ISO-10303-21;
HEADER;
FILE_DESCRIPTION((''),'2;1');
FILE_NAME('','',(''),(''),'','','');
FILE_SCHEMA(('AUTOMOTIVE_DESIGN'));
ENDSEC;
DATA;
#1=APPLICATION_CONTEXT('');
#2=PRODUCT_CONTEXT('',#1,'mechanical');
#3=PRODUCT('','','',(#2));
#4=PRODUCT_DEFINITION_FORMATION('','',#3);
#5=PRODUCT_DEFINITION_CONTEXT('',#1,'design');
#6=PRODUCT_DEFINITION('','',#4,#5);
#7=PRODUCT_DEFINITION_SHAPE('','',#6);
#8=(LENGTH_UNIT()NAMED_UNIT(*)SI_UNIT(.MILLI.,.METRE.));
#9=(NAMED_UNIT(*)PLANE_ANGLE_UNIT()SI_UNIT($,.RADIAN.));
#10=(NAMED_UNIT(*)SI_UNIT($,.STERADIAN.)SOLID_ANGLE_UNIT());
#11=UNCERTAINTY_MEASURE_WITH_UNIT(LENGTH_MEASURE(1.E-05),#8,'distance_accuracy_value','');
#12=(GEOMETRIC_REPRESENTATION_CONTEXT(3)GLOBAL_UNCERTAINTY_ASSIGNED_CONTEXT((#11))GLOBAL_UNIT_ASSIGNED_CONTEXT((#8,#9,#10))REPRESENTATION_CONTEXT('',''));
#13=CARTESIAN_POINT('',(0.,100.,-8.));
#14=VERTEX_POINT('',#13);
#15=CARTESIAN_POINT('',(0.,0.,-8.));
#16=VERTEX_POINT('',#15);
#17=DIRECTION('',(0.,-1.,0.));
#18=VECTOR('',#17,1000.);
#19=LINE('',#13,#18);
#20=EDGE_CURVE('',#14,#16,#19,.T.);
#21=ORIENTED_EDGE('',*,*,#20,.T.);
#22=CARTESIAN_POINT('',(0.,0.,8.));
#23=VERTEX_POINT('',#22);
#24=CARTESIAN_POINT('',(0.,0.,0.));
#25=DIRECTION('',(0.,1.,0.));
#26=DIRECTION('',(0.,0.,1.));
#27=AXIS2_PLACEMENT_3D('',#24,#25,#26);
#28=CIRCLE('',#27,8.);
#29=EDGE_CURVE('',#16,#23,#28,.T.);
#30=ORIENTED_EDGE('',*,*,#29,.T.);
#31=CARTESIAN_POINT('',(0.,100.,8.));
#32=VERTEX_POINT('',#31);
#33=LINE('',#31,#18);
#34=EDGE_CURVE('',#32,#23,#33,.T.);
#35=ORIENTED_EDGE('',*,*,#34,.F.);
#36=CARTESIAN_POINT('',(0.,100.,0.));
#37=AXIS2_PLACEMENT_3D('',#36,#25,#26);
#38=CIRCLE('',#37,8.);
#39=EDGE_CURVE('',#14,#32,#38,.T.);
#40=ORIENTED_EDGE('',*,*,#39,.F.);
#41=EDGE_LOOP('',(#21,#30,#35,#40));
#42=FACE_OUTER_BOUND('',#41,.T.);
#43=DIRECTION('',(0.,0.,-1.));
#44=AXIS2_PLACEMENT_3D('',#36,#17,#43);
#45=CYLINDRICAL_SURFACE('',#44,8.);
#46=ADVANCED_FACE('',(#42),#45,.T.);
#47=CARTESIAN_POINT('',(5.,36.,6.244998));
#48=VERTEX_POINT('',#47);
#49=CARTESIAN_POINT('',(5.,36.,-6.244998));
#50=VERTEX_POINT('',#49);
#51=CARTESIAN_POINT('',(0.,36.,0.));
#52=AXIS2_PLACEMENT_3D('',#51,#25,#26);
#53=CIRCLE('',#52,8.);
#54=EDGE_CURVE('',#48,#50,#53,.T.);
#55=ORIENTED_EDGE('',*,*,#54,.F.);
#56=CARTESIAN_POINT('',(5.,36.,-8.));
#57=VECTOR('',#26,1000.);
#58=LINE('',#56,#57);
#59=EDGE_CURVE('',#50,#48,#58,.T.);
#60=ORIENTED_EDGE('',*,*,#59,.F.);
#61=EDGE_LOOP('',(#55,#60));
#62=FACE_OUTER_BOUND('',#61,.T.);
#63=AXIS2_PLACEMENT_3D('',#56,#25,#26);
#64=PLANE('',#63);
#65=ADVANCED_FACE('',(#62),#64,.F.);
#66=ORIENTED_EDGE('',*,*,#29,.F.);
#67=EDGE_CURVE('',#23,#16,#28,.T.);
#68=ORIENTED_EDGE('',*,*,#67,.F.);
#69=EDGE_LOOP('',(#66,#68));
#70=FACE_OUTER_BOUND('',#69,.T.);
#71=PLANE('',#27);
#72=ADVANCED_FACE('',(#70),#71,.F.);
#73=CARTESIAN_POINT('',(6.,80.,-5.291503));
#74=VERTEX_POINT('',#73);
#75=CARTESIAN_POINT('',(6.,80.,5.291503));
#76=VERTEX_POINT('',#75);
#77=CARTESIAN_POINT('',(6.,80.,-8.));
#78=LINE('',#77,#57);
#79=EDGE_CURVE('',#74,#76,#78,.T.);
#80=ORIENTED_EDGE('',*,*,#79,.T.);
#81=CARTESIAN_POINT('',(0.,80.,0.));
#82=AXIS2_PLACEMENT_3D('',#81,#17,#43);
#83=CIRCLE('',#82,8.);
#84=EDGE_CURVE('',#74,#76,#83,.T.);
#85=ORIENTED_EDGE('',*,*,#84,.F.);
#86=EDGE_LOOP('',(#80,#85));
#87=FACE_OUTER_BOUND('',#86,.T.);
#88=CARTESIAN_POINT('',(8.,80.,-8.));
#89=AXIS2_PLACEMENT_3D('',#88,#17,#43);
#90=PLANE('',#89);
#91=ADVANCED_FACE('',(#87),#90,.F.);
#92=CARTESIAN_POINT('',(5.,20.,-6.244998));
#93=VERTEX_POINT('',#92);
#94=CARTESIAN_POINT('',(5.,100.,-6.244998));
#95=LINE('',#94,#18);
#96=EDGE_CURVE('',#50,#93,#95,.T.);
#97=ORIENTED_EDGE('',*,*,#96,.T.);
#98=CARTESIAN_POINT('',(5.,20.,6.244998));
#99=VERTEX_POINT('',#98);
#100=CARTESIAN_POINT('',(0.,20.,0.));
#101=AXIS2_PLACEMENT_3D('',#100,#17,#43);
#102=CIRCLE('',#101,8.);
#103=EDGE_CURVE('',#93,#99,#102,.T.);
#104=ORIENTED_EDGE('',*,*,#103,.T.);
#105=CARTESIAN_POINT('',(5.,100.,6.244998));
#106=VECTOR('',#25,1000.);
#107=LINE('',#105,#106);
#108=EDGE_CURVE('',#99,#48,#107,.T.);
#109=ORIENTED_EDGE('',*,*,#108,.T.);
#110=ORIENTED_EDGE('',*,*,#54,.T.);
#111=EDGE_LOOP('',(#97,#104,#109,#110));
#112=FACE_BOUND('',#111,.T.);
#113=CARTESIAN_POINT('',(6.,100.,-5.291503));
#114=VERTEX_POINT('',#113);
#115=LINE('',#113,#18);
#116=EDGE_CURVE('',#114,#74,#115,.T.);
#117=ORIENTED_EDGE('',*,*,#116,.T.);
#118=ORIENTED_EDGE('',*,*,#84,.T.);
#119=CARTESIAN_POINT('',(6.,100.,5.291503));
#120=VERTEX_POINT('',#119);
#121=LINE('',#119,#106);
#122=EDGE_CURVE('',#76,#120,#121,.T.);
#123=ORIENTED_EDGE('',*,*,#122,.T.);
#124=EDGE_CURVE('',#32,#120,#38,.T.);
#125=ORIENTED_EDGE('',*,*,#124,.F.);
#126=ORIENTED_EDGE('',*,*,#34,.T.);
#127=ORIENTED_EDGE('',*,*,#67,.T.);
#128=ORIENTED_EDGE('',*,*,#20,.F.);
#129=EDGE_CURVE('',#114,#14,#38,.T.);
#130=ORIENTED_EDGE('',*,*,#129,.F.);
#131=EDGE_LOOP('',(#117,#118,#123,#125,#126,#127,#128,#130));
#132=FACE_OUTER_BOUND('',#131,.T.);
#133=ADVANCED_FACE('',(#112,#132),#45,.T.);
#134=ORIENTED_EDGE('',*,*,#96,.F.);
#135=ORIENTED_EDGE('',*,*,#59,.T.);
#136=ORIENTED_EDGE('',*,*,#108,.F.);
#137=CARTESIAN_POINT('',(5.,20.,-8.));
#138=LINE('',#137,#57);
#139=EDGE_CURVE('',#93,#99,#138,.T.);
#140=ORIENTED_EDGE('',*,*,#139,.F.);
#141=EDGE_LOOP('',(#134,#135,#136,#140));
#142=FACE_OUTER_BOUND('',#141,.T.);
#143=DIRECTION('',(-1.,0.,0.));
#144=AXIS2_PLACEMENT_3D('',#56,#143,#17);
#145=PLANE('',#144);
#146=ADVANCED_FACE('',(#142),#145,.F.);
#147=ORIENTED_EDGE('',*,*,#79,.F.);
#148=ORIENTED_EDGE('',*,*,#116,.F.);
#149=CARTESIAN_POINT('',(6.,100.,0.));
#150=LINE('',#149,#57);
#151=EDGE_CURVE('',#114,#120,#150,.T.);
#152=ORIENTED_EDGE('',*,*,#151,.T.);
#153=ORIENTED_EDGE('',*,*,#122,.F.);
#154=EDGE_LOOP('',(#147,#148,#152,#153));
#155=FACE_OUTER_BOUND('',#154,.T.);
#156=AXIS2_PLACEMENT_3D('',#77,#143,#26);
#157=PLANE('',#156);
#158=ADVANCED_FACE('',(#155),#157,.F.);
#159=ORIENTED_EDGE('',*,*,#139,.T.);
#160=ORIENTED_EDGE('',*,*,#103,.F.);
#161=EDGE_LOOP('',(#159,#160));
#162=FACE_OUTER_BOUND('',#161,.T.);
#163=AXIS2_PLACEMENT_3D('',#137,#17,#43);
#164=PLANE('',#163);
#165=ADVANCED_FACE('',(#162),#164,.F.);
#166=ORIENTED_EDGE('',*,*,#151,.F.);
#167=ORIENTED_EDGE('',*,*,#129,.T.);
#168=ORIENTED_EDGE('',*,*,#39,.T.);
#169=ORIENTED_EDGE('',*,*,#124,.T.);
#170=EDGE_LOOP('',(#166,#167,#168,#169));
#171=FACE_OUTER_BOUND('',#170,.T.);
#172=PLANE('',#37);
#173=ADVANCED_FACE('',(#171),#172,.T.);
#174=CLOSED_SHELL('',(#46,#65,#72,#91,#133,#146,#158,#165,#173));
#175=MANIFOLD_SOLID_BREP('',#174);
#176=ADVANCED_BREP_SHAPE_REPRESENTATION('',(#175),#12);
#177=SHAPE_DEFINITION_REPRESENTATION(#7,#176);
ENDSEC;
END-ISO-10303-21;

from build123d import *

# Parameters (mm, degrees)
SKETCH1_R               = 8
BOSS_EXTRUDE1_DEPTH     = 100
CUT_EXTRUDE1_DEPTH      = 101.637965003
CUT_EXTRUDE1_DEPTH_BACK = 101.637965003
SKETCH2_W               = 2
SKETCH2_H               = 20
SKETCH2_W_2             = 6
SKETCH2_H_2             = 16


with BuildPart() as part:
    # Sketch1 → Boss-Extrude1 (new body)
    with BuildSketch(Plane(origin=(0, 0, 0), x_dir=(1, 0, 0), z_dir=(0, 1, 0))):
        with Locations(Location((0, 0, 0), (0, 0, 270))):
            Circle(SKETCH1_R)
    extrude(amount=BOSS_EXTRUDE1_DEPTH)

    # Sketch2 → Cut-Extrude1 (cut, two sides: drawn at the far end of the back side and taken through both)
    with BuildSketch(Plane.XY.offset(-CUT_EXTRUDE1_DEPTH_BACK)):
        with Locations((7, 90)):
            Rectangle(SKETCH2_W, SKETCH2_H)
        with Locations((8, 28)):
            Rectangle(SKETCH2_W_2, SKETCH2_H_2)
    extrude(amount=CUT_EXTRUDE1_DEPTH + CUT_EXTRUDE1_DEPTH_BACK, mode=Mode.SUBTRACT)


solid = part.part
